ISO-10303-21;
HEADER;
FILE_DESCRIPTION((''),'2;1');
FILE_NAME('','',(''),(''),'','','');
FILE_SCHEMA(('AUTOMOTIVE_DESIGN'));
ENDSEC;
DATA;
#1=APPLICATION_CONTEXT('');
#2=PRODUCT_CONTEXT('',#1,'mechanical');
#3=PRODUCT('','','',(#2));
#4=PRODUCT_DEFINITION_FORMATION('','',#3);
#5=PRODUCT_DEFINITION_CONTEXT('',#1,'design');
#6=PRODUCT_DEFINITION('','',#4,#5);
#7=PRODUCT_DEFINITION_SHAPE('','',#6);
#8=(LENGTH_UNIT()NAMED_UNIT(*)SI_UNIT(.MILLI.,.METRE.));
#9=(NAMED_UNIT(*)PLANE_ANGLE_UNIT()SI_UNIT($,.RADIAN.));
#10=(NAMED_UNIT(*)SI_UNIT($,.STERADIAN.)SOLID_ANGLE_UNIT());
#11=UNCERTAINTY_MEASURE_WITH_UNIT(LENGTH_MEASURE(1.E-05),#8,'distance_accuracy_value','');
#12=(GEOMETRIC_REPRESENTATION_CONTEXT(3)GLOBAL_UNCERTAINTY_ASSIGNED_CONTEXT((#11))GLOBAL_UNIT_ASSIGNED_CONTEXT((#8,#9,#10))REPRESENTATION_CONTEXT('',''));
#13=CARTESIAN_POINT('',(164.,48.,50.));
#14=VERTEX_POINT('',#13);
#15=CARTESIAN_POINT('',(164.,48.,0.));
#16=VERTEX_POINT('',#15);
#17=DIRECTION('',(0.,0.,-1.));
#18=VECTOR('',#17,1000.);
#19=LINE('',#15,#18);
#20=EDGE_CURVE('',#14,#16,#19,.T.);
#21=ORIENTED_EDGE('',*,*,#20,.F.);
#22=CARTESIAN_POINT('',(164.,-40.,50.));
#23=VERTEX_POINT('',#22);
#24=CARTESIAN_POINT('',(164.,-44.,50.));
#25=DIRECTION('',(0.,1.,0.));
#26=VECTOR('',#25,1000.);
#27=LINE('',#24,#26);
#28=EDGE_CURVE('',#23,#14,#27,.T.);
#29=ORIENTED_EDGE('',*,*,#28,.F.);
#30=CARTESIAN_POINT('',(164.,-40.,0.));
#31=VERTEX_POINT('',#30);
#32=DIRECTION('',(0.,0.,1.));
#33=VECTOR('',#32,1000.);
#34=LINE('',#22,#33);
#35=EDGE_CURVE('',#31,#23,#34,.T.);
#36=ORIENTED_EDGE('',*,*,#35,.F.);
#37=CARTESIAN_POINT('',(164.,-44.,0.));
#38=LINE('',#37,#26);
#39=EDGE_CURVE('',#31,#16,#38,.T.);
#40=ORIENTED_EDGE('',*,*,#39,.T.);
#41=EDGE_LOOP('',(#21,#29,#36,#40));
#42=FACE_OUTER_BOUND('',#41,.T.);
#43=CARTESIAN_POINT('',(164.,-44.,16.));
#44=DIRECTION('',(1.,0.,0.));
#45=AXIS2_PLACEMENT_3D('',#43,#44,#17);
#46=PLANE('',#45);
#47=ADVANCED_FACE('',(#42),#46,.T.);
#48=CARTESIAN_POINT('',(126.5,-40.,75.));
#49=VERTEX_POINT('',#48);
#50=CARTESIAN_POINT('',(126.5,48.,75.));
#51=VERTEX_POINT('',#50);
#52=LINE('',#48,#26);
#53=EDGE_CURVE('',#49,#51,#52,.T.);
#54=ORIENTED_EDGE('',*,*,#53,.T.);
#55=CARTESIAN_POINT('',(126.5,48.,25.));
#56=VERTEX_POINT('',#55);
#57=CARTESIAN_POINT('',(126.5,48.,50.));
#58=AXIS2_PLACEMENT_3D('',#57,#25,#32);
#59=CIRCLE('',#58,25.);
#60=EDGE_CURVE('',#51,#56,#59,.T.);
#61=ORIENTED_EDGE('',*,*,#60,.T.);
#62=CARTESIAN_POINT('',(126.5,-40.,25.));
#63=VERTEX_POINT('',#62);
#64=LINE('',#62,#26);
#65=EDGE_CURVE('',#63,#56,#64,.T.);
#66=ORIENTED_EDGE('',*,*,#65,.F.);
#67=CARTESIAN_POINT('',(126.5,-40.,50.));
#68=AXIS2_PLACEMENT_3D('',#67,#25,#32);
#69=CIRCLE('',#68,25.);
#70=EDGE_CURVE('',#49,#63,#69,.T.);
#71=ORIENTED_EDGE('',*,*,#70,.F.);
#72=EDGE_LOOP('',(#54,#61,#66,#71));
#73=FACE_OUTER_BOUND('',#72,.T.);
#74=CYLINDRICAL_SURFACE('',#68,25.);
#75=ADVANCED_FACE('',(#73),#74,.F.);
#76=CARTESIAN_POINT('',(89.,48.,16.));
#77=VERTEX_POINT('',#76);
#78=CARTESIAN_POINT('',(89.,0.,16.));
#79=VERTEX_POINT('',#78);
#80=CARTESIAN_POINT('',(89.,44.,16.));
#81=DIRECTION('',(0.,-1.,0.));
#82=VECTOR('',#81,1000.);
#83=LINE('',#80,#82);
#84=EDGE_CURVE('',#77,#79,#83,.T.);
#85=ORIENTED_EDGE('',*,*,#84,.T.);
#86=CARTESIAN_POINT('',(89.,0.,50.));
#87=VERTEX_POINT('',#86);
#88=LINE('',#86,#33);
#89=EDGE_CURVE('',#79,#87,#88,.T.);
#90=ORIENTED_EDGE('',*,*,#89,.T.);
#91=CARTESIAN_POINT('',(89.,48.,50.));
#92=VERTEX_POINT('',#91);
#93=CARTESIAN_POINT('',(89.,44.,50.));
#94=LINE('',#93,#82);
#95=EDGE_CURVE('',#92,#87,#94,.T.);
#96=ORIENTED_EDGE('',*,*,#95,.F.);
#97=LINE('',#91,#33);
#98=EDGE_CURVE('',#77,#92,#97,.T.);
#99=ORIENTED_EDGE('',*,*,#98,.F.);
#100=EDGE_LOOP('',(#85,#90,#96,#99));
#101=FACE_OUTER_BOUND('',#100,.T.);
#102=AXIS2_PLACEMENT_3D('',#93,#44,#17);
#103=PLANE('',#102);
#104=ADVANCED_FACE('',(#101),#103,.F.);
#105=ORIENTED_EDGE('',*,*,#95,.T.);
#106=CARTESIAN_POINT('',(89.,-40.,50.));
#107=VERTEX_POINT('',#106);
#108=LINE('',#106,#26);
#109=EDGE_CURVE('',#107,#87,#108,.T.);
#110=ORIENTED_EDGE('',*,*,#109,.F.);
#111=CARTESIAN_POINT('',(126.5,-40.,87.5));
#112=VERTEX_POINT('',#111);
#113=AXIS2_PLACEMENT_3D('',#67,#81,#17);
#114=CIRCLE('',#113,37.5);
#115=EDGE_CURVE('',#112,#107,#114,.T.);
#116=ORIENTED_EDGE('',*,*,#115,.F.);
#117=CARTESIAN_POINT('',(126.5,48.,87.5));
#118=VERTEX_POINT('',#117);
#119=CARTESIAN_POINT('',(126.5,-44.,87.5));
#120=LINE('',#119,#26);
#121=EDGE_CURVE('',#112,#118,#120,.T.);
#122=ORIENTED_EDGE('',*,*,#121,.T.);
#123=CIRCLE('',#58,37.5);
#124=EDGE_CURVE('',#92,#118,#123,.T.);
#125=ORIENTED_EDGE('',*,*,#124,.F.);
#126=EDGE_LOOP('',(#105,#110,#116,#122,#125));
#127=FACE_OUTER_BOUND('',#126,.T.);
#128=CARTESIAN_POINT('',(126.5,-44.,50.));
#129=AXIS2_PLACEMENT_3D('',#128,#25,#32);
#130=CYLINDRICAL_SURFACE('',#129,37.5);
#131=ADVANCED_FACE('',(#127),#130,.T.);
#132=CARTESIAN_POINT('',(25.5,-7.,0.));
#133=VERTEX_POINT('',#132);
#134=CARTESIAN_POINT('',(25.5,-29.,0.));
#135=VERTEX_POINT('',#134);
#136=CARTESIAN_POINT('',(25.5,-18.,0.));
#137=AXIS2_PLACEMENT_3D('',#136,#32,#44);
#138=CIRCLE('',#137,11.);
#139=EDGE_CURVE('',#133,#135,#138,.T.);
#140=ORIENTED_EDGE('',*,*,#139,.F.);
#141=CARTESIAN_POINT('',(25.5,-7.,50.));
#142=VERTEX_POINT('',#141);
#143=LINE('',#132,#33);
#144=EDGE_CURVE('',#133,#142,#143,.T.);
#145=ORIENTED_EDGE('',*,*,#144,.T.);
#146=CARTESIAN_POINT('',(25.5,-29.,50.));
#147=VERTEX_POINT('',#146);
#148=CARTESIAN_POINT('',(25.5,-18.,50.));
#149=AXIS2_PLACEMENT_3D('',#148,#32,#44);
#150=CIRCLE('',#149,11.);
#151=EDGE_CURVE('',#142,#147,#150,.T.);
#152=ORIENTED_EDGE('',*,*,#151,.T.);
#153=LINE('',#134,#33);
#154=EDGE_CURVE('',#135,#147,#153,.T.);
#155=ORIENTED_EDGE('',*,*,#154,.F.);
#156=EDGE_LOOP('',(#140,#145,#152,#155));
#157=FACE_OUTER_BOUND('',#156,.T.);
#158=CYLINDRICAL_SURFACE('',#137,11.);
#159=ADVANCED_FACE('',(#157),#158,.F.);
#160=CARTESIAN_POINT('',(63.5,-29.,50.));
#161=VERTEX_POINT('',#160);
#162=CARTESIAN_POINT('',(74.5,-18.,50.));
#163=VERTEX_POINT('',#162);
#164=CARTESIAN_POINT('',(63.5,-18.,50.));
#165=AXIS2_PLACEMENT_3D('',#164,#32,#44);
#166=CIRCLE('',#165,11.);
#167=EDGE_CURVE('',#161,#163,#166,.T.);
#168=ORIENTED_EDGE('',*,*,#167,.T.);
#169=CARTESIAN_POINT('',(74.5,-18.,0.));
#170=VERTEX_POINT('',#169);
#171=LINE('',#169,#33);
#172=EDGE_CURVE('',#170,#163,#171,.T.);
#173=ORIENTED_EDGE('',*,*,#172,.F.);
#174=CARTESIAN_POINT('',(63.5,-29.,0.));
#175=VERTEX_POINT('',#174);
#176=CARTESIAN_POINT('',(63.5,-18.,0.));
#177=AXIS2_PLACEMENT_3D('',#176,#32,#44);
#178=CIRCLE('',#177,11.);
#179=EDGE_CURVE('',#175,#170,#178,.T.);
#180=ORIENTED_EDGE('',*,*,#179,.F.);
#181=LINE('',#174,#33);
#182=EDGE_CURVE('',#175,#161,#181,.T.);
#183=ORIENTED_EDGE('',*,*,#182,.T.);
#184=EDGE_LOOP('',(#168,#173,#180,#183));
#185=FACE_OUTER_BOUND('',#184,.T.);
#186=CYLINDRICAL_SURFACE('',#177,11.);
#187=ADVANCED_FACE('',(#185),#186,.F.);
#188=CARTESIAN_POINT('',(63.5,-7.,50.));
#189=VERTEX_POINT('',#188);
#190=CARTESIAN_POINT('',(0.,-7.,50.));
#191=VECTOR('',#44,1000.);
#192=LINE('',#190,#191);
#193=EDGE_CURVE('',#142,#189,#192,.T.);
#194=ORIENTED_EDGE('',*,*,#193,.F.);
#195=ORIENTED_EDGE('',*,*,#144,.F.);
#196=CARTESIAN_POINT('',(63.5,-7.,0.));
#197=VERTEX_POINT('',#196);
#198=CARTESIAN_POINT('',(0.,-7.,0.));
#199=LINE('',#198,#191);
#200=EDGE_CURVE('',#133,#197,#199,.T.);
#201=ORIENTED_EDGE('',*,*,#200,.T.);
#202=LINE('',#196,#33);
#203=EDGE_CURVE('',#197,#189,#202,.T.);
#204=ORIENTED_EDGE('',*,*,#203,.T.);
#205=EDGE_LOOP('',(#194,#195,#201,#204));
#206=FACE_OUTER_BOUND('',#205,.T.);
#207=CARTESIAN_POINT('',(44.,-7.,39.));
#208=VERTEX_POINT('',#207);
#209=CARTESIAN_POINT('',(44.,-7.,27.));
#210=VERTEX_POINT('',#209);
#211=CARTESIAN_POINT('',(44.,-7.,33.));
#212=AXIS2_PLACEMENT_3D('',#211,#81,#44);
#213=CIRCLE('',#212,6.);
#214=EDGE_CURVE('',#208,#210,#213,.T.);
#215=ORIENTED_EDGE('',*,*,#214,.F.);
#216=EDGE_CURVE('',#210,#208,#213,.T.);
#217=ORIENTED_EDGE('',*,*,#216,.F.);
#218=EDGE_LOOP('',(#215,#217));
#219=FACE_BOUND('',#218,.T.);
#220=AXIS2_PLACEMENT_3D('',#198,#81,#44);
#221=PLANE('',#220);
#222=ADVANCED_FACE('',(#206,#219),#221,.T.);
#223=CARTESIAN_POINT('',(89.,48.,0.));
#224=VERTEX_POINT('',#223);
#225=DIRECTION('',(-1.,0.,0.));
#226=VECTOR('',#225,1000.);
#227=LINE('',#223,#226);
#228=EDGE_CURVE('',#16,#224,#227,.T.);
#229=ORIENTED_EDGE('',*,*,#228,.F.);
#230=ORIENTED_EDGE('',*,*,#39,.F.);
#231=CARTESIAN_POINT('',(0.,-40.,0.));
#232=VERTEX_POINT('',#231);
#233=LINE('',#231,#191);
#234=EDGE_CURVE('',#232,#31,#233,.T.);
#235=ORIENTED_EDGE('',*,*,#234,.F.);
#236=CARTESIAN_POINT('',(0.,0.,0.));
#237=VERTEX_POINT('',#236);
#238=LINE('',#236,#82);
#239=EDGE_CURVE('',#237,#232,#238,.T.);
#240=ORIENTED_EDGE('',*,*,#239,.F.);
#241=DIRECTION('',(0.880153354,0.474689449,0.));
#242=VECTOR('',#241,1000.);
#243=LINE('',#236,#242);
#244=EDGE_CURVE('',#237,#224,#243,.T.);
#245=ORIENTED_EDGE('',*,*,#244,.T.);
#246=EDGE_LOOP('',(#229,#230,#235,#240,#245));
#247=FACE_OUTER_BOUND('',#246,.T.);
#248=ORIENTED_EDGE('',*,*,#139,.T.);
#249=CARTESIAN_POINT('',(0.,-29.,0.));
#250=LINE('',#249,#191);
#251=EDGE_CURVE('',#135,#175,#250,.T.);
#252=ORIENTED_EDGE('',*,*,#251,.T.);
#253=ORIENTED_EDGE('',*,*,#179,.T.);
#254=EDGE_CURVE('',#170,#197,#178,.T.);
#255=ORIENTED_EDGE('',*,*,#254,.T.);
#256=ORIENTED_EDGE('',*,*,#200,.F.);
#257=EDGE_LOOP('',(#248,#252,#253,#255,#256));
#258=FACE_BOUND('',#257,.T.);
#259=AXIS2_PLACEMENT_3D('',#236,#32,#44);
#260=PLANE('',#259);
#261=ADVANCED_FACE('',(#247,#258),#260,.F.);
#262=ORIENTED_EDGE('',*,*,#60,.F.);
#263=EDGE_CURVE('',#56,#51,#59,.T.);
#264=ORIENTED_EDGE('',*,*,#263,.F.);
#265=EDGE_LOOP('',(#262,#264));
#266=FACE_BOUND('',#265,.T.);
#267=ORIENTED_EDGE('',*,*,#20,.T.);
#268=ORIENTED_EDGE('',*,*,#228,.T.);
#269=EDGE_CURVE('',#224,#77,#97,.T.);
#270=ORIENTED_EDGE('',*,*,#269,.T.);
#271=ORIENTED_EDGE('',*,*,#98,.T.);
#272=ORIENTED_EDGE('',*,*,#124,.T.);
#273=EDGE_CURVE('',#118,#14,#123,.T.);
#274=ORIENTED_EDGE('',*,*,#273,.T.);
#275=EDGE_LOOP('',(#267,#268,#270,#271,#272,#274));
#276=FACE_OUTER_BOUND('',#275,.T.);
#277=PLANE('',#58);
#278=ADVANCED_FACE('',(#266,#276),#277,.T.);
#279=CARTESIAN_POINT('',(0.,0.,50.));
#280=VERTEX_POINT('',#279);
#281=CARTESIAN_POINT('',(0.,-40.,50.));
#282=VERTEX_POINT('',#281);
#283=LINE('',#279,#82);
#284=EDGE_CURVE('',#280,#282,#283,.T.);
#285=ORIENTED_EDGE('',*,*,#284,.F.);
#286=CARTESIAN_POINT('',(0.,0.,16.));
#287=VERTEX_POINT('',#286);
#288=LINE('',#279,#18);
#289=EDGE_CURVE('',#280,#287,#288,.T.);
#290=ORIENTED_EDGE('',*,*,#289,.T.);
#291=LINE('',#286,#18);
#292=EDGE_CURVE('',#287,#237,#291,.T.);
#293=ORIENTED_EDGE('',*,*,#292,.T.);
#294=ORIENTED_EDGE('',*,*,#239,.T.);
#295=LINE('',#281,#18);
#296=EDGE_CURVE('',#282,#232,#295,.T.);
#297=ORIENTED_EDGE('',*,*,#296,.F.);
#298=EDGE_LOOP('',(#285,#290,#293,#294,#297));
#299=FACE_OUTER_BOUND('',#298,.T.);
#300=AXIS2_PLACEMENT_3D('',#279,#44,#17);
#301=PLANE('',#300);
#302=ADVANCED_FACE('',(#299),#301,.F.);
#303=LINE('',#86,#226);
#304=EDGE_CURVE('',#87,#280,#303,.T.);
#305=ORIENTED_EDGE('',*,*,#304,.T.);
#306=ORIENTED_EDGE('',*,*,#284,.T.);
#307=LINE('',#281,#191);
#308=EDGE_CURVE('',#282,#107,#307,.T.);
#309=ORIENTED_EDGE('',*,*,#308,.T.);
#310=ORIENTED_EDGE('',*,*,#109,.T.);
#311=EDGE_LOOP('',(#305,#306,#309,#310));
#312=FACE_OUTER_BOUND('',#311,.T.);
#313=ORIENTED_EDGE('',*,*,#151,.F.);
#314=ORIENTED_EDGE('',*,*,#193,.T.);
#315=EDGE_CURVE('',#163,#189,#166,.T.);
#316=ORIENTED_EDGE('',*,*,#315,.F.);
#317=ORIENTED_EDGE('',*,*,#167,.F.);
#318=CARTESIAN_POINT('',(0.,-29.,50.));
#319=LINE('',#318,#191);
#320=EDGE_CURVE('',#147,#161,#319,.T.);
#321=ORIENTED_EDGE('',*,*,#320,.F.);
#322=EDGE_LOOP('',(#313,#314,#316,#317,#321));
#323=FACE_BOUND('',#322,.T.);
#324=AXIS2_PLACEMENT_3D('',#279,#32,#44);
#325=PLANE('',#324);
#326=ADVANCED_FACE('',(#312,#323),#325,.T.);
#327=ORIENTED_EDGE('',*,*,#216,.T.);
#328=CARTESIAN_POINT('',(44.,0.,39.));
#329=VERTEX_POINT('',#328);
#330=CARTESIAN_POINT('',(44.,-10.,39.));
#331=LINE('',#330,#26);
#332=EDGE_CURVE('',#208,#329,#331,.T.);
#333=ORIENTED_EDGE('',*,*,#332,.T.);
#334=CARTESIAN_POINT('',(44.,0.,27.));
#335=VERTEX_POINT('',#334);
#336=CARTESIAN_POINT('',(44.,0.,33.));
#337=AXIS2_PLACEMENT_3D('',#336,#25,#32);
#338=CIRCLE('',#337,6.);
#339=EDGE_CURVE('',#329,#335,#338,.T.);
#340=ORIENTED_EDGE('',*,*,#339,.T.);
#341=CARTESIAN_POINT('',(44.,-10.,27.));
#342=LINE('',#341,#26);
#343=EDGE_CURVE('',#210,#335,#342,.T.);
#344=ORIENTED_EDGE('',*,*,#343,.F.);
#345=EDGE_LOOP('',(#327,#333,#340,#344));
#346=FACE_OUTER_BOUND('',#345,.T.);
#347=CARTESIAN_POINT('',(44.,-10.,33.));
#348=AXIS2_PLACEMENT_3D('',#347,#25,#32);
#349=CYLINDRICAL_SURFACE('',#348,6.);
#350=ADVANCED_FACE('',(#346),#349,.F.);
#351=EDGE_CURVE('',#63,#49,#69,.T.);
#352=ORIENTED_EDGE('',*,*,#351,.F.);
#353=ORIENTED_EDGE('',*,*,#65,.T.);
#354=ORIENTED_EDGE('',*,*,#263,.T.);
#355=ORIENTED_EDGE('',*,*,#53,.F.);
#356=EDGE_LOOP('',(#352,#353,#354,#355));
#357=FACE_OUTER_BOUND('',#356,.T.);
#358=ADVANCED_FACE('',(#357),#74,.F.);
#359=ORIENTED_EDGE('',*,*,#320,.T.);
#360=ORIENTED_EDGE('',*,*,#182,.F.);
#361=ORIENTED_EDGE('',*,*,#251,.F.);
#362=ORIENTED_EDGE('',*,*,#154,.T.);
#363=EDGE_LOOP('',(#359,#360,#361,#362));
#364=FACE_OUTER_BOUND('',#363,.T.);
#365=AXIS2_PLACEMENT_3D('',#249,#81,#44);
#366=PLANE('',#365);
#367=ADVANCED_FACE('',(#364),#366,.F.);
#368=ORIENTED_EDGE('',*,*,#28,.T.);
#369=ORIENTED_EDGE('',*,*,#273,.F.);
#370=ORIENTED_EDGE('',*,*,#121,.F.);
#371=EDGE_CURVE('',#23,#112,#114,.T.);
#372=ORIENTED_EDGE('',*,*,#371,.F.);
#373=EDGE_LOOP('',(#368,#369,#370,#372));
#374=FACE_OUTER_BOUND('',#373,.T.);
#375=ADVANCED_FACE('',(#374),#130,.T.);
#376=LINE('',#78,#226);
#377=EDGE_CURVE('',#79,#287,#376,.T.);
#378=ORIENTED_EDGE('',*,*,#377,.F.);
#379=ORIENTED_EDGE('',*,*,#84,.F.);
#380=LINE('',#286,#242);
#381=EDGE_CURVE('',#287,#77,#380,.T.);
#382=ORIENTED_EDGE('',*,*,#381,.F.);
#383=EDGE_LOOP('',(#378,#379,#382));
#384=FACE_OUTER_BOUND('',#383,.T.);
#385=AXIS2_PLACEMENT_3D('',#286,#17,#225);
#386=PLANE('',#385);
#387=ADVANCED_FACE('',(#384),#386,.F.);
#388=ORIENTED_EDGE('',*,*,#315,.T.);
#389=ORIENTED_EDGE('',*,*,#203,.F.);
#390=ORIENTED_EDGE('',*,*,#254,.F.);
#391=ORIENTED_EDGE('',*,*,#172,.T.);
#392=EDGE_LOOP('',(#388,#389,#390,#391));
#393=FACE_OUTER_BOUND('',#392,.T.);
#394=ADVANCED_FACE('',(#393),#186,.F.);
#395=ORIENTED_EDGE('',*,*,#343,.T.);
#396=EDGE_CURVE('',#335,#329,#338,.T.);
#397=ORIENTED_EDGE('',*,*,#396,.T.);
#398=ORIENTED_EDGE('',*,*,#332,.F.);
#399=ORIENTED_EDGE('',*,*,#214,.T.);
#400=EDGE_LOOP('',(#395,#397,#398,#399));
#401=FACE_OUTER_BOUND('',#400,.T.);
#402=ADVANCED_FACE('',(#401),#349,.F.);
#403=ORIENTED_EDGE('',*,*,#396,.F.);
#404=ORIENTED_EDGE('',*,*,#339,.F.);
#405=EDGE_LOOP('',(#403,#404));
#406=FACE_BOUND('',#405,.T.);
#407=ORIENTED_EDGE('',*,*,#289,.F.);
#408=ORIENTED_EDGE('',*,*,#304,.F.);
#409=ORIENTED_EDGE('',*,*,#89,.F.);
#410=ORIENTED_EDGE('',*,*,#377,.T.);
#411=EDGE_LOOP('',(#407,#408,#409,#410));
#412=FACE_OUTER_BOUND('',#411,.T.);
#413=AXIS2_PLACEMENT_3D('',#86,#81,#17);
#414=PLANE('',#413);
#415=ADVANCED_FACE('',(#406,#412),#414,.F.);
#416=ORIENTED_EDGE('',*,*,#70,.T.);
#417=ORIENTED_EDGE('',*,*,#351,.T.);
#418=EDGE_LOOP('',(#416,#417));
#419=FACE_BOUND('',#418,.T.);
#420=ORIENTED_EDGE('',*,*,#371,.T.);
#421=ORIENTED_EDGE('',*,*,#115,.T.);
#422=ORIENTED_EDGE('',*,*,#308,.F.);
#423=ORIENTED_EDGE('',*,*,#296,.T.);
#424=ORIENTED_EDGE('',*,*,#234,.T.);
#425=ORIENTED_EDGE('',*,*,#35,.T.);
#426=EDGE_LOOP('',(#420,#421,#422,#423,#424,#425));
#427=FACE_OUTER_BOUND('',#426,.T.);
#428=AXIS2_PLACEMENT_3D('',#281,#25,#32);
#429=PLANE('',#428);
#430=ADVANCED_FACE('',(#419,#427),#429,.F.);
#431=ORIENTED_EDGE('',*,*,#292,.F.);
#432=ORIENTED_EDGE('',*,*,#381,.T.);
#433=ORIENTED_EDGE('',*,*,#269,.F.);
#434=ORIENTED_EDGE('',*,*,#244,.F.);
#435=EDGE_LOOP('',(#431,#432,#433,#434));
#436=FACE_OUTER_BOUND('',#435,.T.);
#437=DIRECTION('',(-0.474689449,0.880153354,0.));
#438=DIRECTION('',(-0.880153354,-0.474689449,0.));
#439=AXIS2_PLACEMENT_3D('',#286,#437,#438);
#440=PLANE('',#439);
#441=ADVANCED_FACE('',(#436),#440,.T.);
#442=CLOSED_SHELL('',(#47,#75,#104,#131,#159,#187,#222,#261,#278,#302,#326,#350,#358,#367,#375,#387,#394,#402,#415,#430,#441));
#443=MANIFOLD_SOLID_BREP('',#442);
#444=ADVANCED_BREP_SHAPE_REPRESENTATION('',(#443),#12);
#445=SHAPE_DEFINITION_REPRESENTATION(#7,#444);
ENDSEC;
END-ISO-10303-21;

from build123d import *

# Parameters (mm, degrees)
BASE_BLOCK_SKETCH_W       = 89
BASE_BLOCK_SKETCH_H       = 40
BASE_BLOCK_50MM_DEPTH     = 50
ROUNDED_BOSS_44MM_DEPTH   = 44
BOSS_START                = 44
BOSS_EXTENSION_44MM_DEPTH = 44
GUSSET_A_16MM_DEPTH       = 16
RECESS_START              = -4
RECESS_4MM_DEPTH          = 4
PAD_START                 = 4
PAD_4MM_DEPTH             = 4
GUSSET_B_16MM_DEPTH       = 16
BORE_SKETCH_50_R          = 25
BORE_50_DEPTH             = 88
SIDE_SLOT_DEPTH           = 50
HOLE_SKETCH_12_R          = 6
HOLE_12_DEPTH             = 10


with BuildPart() as part:
    # Base Block Sketch → Base Block 50mm (new body)
    with BuildSketch(Plane.XY):
        with Locations((44.5, -20)):
            Rectangle(BASE_BLOCK_SKETCH_W, BASE_BLOCK_SKETCH_H)
    extrude(amount=BASE_BLOCK_50MM_DEPTH)

    # Rounded Boss Sketch → Rounded Boss 44mm (add)
    with BuildSketch(Plane(origin=(0, 0, 0), x_dir=(1, 0, 0), z_dir=(0, 1, 0))):
        with BuildLine():
            Line((89, 0), (89, -16))
            Line((89, -16), (89, -50))
            ThreePointArc((89, -50), (126.5, -87.5), (164, -50))
            Line((164, -50), (164, -16))
            Line((164, -16), (164, 0))
            Line((164, 0), (89, 0))
        make_face()
    extrude(amount=-ROUNDED_BOSS_44MM_DEPTH)

    # Boss Extension Sketch → Boss Extension 44mm (add)
    with BuildSketch(Plane(origin=(0, 0, 0), x_dir=(1, 0, 0), z_dir=(0, 1, 0)).offset(BOSS_START)):
        with BuildLine():
            Line((164, 0), (164, -50))
            ThreePointArc((164, -50), (126.5, -87.5), (89, -50))
            Line((89, -50), (89, 0))
            Line((89, 0), (164, 0))
        make_face()
    extrude(amount=-BOSS_EXTENSION_44MM_DEPTH)

    # Gusset A Sketch → Gusset A 16mm (add)
    with BuildSketch(Plane(origin=(0, 0, 0), x_dir=(-1, 0, 0), z_dir=(0, 0, -1))):
        Polygon((-89, 44), (-89, 0), (0, 0), align=None)
    extrude(amount=-GUSSET_A_16MM_DEPTH)

    # Recess Sketch → Recess 4mm (cut)
    with BuildSketch(Plane.XZ.offset(44).offset(RECESS_START)):
        with BuildLine():
            Line((89, 0), (89, 50))
            ThreePointArc((89, 50), (126.5, 87.5), (164, 50))
            Line((164, 50), (164, 0))
            Line((164, 0), (89, 0))
        make_face()
    extrude(amount=RECESS_4MM_DEPTH, mode=Mode.SUBTRACT)

    # Pad Sketch → Pad 4mm (add)
    with BuildSketch(Plane(origin=(0, 44, 0), x_dir=(1, 0, 0), z_dir=(0, 1, 0)).offset(PAD_START)):
        with BuildLine():
            Line((89, 0), (164, 0))
            Line((164, 0), (164, -50))
            ThreePointArc((164, -50), (126.5, -87.5), (89, -50))
            Line((89, -50), (89, 0))
        make_face()
    extrude(amount=-PAD_4MM_DEPTH)

    # Gusset B Sketch → Gusset B 16mm (add)
    with BuildSketch(Plane(origin=(0, 0, 0), x_dir=(-1, 0, 0), z_dir=(0, 0, -1))):
        Polygon((-89, 48), (-89, 44), (0, 0), align=None)
    extrude(amount=-GUSSET_B_16MM_DEPTH)

    # Bore Sketch Ø50 → Bore Ø50 (cut)
    with BuildSketch(Plane(origin=(0, 48, 0), x_dir=(1, 0, 0), z_dir=(0, 1, 0))):
        with Locations(Location((126.5, -50, 0), (0, 0, 270))):
            Circle(BORE_SKETCH_50_R)
    extrude(amount=-BORE_50_DEPTH, mode=Mode.SUBTRACT)

    # Side Slot Sketch → Side Slot (cut)
    with BuildSketch(Plane.XY.offset(50)):
        with BuildLine():
            Line((25.5, -29), (63.5, -29))
            ThreePointArc((63.5, -29), (74.5, -18), (63.5, -7))
            Line((63.5, -7), (25.5, -7))
            ThreePointArc((25.5, -7), (14.5, -18), (25.5, -29))
        make_face()
    extrude(amount=-SIDE_SLOT_DEPTH, mode=Mode.SUBTRACT)

    # Hole Sketch Ø12 → Hole Ø12 (cut)
    with BuildSketch(Plane(origin=(0, 0, 0), x_dir=(1, 0, 0), z_dir=(0, 1, 0))):
        with Locations(Location((44, -33, 0), (0, 0, 270))):
            Circle(HOLE_SKETCH_12_R)
    extrude(amount=-HOLE_12_DEPTH, mode=Mode.SUBTRACT)


solid = part.part
